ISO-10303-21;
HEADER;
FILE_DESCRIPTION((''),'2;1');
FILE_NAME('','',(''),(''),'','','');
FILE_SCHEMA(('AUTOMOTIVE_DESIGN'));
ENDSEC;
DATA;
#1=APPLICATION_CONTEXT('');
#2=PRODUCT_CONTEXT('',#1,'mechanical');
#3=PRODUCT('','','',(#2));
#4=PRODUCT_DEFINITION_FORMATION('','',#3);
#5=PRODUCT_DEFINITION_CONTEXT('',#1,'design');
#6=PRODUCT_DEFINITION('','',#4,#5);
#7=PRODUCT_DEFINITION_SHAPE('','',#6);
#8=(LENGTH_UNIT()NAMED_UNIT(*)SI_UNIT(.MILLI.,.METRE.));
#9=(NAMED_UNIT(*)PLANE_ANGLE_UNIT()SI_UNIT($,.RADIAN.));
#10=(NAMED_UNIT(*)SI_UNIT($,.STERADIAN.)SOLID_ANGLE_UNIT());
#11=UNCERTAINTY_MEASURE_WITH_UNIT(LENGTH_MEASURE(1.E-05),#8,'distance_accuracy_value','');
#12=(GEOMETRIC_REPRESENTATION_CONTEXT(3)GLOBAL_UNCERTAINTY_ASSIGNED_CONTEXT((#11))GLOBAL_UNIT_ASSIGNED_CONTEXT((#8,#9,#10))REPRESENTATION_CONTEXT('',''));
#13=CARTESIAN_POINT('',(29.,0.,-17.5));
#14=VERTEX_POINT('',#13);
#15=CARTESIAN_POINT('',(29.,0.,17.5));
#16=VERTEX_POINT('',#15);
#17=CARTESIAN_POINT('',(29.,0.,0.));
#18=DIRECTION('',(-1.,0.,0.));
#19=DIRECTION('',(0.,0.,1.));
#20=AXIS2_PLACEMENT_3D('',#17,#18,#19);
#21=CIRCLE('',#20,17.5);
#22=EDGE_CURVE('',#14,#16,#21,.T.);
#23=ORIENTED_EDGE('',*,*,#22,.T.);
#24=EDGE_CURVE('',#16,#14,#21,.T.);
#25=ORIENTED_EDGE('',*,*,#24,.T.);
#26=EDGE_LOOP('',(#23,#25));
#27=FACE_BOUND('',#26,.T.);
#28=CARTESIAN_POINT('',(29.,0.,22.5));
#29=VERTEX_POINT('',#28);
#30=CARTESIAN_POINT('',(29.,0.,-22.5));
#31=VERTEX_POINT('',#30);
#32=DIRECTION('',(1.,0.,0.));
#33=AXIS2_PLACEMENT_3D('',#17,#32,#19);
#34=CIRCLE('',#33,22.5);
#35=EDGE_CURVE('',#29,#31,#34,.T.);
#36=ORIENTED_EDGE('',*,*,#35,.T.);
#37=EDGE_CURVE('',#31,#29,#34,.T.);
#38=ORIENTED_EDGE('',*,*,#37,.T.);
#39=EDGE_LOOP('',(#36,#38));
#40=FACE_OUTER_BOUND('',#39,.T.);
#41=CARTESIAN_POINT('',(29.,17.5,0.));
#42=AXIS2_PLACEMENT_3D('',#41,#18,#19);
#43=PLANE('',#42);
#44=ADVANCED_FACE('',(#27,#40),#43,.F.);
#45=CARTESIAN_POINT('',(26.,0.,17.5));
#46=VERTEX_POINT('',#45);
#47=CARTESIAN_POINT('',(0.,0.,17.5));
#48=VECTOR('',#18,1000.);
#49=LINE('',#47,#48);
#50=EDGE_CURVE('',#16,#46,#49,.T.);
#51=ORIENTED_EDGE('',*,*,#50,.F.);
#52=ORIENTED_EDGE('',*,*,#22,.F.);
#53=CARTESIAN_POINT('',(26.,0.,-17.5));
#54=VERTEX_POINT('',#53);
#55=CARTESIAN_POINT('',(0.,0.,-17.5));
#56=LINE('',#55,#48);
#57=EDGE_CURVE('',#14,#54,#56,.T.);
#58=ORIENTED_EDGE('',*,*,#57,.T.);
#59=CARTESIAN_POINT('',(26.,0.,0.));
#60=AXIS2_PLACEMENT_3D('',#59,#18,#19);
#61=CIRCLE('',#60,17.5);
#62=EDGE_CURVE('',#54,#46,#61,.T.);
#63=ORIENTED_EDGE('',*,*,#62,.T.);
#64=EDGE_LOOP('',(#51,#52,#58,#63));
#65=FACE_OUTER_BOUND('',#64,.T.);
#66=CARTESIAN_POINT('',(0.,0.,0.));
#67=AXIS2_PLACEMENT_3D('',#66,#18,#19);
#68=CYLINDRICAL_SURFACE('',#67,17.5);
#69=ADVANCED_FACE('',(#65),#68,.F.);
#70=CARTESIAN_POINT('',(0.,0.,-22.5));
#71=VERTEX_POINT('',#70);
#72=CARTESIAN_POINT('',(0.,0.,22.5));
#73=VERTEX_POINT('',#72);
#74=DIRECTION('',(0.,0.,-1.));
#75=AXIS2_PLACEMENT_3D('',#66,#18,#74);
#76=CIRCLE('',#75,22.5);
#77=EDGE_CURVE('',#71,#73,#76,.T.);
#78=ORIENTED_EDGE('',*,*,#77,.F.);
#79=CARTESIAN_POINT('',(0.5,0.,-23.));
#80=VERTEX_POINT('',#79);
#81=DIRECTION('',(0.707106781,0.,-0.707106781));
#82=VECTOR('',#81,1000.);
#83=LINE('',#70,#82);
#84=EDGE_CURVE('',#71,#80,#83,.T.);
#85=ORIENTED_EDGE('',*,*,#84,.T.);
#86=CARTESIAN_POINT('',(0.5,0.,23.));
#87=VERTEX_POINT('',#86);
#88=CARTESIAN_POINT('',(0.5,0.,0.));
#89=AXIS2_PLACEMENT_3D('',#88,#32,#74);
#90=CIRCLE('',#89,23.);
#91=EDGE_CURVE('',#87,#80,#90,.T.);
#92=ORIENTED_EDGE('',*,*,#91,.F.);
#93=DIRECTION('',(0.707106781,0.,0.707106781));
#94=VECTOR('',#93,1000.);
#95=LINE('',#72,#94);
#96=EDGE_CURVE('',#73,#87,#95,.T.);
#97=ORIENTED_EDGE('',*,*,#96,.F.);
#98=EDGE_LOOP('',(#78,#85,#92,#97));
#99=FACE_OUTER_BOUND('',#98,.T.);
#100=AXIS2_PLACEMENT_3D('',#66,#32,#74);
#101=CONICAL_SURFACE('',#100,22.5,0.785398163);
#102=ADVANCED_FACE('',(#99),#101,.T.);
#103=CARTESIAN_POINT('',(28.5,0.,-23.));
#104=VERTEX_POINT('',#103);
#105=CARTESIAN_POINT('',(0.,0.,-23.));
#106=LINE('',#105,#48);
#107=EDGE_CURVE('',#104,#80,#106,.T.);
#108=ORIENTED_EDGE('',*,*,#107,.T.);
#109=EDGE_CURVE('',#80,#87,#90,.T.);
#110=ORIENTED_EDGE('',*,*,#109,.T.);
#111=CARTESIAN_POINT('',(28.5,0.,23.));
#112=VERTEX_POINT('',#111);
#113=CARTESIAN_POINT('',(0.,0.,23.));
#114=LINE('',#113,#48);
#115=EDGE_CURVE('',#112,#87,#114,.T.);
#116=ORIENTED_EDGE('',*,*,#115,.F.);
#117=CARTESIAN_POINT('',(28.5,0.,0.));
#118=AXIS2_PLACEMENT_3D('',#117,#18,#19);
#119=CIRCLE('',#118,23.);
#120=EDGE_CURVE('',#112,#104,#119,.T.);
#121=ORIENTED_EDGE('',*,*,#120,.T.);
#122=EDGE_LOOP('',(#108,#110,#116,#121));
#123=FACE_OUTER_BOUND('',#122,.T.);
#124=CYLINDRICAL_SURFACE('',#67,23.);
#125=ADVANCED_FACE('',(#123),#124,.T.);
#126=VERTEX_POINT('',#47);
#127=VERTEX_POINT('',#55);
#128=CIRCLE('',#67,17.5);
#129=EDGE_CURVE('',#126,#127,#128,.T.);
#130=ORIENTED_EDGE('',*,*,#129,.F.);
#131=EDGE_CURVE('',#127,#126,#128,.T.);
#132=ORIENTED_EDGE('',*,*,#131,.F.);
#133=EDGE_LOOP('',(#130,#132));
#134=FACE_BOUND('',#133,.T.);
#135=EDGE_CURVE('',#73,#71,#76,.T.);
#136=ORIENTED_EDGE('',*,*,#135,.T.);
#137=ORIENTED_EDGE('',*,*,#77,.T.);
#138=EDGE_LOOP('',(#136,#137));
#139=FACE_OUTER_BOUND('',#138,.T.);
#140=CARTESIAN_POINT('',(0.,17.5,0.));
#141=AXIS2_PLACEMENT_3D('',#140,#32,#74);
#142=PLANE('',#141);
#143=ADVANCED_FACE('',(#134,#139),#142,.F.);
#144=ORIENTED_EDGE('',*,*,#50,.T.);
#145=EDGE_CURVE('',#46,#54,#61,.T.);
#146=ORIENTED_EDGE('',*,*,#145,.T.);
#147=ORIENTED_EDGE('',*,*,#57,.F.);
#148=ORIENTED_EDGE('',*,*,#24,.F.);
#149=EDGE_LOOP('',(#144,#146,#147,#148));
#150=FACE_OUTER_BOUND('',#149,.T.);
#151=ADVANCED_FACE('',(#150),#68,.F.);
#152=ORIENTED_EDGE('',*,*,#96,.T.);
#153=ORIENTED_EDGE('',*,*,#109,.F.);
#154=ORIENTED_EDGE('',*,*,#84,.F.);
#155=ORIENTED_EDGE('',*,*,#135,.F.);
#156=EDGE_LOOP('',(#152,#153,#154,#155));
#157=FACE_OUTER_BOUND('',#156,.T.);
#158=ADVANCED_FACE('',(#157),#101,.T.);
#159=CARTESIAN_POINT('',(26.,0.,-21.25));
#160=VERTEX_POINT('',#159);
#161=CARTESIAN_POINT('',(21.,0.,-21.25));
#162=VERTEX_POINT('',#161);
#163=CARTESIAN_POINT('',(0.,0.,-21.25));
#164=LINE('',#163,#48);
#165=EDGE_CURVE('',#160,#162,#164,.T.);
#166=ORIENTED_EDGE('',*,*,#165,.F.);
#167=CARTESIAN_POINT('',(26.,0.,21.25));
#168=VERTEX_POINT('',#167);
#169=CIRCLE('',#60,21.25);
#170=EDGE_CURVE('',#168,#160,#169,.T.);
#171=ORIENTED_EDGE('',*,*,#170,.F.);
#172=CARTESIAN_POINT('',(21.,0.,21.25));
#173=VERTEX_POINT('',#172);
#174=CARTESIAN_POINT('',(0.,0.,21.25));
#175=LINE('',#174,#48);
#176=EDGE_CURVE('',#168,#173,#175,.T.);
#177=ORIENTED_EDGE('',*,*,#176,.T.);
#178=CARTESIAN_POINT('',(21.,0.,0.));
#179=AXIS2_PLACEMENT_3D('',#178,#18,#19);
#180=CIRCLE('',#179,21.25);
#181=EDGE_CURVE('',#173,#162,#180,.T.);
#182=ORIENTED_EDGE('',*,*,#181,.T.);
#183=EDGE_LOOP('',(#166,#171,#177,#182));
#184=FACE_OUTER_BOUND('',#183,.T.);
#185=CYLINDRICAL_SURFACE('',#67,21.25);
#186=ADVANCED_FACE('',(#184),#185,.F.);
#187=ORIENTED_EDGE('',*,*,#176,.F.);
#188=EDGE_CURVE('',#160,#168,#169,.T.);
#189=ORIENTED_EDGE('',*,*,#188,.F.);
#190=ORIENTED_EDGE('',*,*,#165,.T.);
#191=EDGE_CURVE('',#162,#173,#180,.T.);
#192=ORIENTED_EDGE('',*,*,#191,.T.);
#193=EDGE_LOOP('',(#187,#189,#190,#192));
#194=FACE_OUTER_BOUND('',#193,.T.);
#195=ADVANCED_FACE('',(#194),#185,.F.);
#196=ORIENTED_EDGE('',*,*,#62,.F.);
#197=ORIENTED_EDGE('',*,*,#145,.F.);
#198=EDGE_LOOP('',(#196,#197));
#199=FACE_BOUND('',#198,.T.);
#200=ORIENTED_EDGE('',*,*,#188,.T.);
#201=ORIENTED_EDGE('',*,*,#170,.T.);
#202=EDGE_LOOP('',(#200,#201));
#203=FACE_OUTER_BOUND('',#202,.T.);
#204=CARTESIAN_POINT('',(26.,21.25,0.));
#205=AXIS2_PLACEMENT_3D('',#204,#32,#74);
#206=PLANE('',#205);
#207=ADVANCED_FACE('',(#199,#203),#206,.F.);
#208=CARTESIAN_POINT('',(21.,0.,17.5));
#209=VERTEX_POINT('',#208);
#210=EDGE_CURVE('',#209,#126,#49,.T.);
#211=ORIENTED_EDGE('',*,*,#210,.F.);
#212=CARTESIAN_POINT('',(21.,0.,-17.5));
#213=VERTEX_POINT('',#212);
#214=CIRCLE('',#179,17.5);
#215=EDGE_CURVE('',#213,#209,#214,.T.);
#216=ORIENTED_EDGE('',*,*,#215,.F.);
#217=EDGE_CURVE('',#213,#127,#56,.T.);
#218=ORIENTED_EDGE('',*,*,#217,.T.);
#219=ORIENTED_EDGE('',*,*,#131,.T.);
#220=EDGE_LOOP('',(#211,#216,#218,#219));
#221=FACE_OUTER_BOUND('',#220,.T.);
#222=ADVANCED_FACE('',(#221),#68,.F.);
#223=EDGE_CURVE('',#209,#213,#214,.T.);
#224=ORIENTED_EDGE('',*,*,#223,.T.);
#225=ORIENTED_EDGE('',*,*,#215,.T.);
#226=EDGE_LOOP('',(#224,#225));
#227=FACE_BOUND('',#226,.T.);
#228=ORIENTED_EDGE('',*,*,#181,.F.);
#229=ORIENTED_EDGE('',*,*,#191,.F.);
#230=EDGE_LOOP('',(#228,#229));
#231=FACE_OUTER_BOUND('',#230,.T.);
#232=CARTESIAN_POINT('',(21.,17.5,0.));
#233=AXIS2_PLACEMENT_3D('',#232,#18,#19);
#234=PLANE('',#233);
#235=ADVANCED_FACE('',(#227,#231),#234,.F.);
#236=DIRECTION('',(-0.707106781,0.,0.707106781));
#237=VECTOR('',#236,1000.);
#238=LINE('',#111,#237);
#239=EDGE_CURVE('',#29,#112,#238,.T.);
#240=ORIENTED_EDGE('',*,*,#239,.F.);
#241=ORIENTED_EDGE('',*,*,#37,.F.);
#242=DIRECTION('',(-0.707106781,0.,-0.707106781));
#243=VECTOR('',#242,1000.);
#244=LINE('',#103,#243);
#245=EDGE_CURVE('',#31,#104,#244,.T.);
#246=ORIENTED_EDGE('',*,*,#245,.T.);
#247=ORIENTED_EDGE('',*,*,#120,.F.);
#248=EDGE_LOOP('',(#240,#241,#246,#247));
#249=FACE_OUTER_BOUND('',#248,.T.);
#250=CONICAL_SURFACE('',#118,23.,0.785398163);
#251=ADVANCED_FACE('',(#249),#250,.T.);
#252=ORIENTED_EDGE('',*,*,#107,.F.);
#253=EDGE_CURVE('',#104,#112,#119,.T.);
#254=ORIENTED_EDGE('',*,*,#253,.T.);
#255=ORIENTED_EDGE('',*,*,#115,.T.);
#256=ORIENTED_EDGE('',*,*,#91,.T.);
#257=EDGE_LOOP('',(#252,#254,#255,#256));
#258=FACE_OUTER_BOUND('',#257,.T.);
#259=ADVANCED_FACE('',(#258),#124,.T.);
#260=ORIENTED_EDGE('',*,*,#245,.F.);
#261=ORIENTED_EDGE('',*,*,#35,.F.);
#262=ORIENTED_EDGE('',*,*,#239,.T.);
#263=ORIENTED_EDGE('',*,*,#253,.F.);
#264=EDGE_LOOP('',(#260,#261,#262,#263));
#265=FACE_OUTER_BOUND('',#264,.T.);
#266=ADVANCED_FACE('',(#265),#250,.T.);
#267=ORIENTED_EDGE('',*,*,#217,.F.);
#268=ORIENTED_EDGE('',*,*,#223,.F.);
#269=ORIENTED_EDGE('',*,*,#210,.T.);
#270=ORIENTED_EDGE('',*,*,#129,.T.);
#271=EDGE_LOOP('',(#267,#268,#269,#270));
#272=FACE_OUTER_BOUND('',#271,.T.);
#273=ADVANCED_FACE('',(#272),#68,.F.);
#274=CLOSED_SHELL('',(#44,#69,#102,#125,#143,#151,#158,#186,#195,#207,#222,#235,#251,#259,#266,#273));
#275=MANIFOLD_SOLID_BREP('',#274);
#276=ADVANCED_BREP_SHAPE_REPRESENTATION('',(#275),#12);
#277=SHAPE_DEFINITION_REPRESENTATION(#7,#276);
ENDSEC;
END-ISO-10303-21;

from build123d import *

# Parameters (mm, degrees)
CHAMFER_1_SIZE = 0.5


with BuildPart() as part:
    # 草图1 → 旋转1 (revolve)
    with BuildSketch(Plane.XY, mode=Mode.PRIVATE) as revolve_1_sk:
        Polygon((0, 17.5), (21, 17.5), (21, 21.25), (26, 21.25), (26, 17.5), (29, 17.5), (29, 23), (0, 23), align=None)
    revolve(revolve_1_sk.sketch.rotate(Axis((0, 0, 0), (1, 0, 0)), 90), axis=Axis((0, 0, 0), (1, 0, 0)))

    # 倒角1
    chamfer_1_edges = [part.edges().sort_by_distance(p)[0] for p in [
        (29, 0, -23),
        (0, 0, -23),
    ]]
    chamfer(chamfer_1_edges, length=CHAMFER_1_SIZE)


solid = part.part
